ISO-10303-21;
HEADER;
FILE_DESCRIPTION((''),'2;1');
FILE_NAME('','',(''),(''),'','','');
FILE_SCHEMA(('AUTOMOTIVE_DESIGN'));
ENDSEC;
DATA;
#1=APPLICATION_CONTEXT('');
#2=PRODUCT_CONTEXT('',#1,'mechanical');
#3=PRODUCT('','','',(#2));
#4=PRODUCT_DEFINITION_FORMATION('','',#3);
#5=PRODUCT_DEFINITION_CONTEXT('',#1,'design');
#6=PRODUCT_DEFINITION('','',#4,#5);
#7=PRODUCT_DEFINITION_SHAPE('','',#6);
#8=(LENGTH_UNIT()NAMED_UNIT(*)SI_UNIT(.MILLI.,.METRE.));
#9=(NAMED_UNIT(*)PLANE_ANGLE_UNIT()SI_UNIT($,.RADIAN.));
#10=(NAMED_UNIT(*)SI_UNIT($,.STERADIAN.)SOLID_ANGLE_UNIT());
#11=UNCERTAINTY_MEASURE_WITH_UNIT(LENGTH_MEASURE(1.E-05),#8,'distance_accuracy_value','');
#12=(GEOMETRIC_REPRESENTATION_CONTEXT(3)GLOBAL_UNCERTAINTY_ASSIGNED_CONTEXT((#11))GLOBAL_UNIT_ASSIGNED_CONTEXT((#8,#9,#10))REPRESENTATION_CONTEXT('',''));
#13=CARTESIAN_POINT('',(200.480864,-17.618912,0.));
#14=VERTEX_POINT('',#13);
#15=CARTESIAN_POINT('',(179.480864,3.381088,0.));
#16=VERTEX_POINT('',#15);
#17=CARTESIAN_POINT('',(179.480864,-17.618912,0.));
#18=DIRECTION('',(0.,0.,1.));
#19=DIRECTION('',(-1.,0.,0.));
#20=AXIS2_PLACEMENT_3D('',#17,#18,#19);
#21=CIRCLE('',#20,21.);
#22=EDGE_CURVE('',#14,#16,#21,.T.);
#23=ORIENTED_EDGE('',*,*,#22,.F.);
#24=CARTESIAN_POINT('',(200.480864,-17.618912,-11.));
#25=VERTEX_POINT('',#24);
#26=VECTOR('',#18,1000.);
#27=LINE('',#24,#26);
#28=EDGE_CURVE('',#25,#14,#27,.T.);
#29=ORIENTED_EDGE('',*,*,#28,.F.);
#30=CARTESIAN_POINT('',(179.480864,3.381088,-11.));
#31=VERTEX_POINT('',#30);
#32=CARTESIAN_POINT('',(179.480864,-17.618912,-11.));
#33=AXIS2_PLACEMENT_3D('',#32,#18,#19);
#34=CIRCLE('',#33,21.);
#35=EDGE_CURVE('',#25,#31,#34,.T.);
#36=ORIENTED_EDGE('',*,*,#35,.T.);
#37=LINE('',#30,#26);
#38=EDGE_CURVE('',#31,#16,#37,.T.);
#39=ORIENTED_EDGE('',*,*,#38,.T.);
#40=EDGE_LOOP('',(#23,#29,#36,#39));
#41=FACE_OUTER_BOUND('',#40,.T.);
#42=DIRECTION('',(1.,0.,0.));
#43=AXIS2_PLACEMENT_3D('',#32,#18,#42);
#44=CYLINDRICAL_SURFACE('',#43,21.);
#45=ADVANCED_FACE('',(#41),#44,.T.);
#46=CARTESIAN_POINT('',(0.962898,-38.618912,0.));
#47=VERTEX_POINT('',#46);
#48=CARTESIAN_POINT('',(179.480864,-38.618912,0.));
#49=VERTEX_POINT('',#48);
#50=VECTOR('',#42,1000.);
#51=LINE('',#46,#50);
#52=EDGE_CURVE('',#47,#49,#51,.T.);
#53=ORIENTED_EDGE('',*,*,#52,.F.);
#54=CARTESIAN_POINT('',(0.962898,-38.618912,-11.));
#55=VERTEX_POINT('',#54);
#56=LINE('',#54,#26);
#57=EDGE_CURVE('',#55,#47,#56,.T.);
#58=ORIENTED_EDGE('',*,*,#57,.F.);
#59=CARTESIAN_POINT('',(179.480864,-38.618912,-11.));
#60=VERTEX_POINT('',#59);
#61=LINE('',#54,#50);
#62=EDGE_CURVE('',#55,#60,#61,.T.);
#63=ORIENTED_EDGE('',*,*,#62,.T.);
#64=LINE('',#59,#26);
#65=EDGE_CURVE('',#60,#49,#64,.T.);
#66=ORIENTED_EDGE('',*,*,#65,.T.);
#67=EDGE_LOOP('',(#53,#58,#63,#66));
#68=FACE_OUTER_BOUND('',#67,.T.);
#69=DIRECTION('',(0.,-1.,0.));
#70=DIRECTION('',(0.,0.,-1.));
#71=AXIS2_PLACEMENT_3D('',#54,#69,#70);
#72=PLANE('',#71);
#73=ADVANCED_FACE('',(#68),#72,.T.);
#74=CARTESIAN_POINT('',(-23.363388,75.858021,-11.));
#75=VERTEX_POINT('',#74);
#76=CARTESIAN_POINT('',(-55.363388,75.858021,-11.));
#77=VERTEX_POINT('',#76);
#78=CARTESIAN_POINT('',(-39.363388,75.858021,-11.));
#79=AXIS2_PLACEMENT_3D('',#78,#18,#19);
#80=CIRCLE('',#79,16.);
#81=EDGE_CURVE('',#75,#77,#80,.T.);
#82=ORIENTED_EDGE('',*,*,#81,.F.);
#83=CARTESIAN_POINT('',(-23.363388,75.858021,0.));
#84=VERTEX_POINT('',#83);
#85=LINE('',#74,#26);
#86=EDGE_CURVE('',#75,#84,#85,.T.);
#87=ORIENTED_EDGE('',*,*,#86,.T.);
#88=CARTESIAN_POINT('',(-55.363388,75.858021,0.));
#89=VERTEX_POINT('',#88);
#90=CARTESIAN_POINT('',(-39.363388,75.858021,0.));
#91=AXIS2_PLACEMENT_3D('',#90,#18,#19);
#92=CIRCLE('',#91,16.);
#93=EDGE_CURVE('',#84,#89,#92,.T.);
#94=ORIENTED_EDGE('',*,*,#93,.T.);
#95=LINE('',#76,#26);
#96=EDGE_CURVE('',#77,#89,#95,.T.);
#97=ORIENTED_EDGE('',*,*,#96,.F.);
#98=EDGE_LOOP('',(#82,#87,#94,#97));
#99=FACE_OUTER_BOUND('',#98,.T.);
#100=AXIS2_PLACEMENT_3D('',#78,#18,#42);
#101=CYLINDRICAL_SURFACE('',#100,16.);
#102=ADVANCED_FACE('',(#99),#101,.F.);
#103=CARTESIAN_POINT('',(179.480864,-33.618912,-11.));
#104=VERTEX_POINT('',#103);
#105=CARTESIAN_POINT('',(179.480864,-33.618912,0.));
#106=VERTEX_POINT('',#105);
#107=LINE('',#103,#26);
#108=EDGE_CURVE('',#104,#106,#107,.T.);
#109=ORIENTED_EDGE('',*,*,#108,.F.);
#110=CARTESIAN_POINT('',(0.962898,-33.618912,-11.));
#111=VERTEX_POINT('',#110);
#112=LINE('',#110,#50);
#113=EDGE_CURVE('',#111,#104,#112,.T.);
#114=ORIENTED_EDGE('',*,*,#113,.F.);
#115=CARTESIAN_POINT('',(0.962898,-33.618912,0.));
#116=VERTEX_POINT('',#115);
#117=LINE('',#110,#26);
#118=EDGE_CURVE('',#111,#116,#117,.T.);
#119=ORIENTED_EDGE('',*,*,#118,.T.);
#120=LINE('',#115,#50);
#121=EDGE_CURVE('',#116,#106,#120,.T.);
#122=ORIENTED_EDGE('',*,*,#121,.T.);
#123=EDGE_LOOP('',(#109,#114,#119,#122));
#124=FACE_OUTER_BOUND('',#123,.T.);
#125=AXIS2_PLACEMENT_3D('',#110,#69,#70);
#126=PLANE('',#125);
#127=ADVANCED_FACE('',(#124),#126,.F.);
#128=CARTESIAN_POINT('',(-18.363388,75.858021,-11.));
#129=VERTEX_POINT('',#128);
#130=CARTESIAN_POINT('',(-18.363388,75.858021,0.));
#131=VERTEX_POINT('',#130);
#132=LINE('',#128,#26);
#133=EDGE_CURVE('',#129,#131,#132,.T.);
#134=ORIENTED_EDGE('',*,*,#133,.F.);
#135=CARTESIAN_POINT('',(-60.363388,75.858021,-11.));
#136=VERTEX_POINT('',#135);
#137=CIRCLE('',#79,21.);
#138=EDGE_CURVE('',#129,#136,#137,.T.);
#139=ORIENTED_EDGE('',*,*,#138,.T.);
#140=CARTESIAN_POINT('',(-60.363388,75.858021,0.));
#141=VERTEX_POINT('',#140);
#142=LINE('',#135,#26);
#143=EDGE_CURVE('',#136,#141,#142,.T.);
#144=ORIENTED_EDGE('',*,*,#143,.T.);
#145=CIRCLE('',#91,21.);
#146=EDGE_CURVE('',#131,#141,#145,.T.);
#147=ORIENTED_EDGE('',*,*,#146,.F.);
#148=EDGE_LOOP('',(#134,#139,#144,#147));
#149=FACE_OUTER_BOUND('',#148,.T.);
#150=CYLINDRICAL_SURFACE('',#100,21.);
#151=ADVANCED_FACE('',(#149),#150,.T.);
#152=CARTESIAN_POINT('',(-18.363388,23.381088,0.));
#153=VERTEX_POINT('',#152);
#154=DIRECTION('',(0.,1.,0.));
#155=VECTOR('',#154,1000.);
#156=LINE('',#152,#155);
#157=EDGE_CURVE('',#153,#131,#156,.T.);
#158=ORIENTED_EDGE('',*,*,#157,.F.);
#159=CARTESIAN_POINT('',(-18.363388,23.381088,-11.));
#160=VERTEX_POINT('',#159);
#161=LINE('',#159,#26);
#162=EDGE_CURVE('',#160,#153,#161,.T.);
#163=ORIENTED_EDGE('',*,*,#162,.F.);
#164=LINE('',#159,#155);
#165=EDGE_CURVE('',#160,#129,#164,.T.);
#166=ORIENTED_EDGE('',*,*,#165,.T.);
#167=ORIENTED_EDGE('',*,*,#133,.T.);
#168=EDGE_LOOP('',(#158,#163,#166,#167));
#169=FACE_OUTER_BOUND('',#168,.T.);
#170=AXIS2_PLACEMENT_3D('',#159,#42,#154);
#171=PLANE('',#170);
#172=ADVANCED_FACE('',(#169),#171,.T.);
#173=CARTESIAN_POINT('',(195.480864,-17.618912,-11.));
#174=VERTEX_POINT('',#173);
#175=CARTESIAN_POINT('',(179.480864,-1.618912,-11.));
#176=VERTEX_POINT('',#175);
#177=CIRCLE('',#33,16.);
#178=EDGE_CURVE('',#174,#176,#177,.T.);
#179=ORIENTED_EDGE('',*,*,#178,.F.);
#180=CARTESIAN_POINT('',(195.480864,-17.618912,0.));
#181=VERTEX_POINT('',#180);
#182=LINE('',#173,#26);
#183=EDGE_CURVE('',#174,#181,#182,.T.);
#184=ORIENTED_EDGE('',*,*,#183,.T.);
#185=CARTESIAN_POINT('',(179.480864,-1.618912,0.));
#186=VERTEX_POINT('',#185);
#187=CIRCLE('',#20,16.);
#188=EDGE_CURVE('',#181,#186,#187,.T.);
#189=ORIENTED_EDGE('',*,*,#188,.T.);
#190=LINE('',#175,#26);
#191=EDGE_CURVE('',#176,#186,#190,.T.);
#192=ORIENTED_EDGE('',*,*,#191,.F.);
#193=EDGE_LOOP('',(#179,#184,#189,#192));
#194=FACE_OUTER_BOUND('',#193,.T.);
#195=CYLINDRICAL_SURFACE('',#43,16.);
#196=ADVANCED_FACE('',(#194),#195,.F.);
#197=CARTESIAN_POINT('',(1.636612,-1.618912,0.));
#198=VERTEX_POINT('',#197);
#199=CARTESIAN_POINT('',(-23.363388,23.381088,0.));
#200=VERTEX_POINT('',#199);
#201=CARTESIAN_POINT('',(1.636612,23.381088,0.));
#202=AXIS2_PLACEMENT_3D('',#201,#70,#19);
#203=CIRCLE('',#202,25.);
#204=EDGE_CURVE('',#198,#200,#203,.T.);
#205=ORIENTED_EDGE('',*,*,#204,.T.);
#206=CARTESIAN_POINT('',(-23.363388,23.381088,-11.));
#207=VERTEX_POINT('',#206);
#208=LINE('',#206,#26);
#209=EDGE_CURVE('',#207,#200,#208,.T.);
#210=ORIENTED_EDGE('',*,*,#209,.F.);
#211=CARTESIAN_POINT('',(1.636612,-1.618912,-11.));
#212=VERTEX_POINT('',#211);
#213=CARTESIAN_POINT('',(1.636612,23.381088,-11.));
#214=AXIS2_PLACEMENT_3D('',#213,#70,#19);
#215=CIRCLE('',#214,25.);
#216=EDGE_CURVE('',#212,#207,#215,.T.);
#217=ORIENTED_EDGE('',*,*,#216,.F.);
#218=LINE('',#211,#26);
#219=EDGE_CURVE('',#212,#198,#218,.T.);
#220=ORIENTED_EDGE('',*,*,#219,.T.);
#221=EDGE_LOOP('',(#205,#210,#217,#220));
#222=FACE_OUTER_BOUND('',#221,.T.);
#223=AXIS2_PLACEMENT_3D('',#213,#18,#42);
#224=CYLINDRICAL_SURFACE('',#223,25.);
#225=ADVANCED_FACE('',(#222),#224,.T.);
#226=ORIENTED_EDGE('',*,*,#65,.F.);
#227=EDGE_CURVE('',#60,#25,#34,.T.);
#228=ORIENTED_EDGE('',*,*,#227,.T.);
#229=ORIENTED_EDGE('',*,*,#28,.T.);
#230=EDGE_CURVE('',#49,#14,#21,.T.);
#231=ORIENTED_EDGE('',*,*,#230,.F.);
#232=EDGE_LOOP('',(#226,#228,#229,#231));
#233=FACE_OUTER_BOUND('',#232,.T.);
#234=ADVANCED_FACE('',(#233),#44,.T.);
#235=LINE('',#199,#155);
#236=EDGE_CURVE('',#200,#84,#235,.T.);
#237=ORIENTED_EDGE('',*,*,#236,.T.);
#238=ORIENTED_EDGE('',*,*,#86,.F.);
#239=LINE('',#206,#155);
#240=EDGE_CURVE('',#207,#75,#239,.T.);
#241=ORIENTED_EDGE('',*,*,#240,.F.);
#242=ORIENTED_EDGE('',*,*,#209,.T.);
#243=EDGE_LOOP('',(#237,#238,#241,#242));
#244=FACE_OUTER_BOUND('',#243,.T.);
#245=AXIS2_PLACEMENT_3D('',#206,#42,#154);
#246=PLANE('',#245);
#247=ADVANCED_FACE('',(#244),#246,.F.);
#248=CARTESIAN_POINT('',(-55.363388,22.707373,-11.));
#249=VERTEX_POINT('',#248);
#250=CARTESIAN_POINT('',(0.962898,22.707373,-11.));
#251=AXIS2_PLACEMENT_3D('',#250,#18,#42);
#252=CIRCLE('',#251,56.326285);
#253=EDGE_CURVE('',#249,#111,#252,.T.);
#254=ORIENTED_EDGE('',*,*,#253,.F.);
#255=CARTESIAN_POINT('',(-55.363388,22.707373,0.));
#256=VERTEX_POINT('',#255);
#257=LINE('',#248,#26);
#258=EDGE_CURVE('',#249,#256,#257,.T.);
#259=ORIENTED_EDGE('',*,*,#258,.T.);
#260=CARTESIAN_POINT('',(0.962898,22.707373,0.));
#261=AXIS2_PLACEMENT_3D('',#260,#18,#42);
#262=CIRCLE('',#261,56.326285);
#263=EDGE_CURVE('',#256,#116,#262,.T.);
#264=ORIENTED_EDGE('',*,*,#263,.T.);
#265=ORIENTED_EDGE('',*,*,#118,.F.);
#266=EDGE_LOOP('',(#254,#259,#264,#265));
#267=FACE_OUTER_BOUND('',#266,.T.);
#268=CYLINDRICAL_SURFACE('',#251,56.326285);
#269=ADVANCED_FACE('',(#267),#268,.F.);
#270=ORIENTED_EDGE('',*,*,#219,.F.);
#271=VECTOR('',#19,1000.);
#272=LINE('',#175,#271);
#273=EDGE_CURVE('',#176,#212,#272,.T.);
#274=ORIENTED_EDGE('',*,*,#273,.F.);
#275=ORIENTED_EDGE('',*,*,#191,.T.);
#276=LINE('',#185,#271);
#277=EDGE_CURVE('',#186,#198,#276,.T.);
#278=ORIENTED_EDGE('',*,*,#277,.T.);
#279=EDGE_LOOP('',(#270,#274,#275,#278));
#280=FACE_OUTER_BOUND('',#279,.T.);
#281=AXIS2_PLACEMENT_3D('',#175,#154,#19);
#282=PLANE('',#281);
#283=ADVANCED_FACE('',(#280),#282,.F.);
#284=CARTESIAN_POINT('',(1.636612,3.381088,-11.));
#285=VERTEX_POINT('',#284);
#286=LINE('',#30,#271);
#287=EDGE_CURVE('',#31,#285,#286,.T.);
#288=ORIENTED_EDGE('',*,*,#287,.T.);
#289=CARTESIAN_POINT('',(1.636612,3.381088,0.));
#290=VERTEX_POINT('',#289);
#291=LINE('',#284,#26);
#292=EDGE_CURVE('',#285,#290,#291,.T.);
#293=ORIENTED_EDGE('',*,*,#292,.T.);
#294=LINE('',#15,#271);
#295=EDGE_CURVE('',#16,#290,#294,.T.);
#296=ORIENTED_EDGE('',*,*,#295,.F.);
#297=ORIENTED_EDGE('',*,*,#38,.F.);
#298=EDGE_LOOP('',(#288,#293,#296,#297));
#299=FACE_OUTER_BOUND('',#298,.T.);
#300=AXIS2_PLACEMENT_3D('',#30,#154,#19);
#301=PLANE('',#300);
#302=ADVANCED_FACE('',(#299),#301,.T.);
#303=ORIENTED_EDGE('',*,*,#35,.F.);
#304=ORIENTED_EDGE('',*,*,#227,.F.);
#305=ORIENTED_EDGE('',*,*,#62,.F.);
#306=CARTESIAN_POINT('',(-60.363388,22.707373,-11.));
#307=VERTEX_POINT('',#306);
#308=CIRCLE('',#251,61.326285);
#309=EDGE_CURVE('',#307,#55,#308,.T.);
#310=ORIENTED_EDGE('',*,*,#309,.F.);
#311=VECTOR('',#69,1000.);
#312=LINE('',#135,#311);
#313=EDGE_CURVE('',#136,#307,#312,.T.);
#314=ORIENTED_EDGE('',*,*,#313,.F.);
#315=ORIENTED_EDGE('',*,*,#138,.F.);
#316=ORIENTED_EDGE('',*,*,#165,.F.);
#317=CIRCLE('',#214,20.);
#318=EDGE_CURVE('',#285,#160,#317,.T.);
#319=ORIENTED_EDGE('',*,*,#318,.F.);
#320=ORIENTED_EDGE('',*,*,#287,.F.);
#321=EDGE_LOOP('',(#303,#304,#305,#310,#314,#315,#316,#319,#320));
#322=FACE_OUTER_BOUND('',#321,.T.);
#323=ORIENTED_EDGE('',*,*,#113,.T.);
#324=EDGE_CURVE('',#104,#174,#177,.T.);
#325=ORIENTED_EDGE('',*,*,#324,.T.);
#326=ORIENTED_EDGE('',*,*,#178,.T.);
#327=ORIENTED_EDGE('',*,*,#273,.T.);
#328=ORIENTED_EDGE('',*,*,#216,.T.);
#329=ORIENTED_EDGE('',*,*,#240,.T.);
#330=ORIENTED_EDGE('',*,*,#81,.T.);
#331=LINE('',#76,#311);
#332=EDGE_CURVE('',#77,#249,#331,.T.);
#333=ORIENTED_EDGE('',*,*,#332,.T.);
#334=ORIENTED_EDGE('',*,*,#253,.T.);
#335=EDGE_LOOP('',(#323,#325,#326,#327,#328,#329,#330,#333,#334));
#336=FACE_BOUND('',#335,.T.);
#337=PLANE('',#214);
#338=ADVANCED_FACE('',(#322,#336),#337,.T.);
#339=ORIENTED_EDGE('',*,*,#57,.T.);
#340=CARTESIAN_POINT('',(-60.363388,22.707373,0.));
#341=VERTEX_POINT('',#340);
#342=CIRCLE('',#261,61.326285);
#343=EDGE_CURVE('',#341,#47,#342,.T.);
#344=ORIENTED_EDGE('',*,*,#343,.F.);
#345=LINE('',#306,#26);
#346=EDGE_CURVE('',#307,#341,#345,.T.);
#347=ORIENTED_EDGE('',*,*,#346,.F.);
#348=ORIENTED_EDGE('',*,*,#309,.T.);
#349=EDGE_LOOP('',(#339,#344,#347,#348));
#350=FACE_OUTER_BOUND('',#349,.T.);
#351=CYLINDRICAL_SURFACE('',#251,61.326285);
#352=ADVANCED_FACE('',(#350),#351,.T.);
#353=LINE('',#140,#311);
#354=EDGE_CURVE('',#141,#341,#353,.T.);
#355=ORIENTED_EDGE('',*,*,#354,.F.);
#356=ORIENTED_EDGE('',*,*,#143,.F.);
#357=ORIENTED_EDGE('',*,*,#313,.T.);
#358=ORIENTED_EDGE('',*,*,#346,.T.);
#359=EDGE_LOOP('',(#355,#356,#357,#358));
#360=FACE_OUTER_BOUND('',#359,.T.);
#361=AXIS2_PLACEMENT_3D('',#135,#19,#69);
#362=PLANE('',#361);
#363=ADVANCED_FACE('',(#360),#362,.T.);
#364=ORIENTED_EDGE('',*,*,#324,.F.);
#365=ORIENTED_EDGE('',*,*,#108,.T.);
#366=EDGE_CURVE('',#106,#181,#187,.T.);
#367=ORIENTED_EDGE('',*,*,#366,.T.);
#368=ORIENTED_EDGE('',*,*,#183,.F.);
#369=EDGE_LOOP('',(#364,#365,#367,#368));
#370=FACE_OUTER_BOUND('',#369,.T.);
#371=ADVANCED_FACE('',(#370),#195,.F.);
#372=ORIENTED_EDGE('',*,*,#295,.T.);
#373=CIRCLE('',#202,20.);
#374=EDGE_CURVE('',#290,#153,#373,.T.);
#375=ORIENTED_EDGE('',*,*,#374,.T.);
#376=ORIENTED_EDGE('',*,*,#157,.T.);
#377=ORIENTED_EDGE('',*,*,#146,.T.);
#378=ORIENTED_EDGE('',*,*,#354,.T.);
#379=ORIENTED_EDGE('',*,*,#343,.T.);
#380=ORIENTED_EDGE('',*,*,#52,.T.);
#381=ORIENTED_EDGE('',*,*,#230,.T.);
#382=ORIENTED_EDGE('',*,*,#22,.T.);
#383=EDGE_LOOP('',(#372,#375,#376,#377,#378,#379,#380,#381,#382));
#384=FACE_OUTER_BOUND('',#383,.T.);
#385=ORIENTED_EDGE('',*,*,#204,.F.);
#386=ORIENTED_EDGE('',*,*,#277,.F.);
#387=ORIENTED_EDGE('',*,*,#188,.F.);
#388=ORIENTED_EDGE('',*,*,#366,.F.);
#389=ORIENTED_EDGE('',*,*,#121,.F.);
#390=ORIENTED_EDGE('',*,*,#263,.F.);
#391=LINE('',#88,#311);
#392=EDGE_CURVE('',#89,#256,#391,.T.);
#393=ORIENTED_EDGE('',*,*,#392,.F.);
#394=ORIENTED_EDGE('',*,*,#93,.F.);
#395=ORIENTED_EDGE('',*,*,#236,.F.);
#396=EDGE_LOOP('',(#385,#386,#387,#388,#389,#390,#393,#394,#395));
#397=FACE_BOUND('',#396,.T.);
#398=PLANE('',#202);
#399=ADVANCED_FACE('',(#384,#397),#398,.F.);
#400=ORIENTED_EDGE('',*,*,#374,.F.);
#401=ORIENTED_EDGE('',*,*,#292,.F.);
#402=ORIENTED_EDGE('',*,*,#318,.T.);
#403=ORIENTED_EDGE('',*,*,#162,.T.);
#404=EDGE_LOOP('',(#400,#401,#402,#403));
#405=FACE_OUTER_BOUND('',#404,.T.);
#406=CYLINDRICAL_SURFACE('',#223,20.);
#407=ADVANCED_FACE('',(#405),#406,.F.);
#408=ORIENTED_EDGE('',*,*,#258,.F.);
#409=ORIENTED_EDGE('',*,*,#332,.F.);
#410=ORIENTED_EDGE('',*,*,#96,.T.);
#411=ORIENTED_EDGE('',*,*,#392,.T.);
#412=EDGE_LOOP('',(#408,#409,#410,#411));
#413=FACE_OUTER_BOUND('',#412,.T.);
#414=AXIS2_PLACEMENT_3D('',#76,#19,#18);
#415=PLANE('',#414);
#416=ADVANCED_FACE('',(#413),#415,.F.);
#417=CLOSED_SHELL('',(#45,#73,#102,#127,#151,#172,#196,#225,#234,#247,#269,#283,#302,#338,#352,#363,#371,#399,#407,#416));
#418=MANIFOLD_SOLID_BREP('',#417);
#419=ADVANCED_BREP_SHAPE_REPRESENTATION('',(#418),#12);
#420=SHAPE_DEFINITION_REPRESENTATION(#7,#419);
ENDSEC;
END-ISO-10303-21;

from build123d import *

# Parameters (mm, degrees)
BOSS_EXTRUDE1_DEPTH = 11


with BuildPart() as part:
    # Sketch1 → Boss-Extrude1 (new body)
    with BuildSketch(Plane.XY):
        with BuildLine():
            Line((-18.363387922, 23.381087781), (-18.363387922, 75.858020773))
            ThreePointArc((-18.363387922, 75.858020773), (-39.363387922, 96.858020773), (-60.363387922, 75.858020773))
            Line((-60.363387922, 75.858020773), (-60.363387922, 22.707373273))
            ThreePointArc((-60.363387922, 22.707373273), (-42.401334766, -20.656859064), (0.962897571, -38.618912219))
            Line((0.962897571, -38.618912219), (179.480864488, -38.618912219))
            ThreePointArc((179.480864488, -38.618912219), (200.480864488, -17.618912219), (179.480864488, 3.381087781))
            Line((179.480864488, 3.381087781), (1.636612078, 3.381087781))
            ThreePointArc((1.636612078, 3.381087781), (-12.505523546, 9.238952157), (-18.363387922, 23.381087781))
        make_face()
        with BuildLine():
            Line((-55.363387922, 75.858020773), (-55.363387922, 22.707373273))
            ThreePointArc((-55.363387922, 22.707373273), (-38.86580086, -17.121325158), (0.962897571, -33.618912219))
            Line((0.962897571, -33.618912219), (179.480864488, -33.618912219))
            ThreePointArc((179.480864488, -33.618912219), (195.480864488, -17.618912219), (179.480864488, -1.618912219))
            Line((179.480864488, -1.618912219), (1.636612078, -1.618912219))
            ThreePointArc((1.636612078, -1.618912219), (-16.041057452, 5.703418251), (-23.363387922, 23.381087781))
            Line((-23.363387922, 23.381087781), (-23.363387922, 75.858020773))
            ThreePointArc((-23.363387922, 75.858020773), (-39.363387922, 91.858020773), (-55.363387922, 75.858020773))
        make_face(mode=Mode.SUBTRACT)
    extrude(amount=-BOSS_EXTRUDE1_DEPTH)


solid = part.part
